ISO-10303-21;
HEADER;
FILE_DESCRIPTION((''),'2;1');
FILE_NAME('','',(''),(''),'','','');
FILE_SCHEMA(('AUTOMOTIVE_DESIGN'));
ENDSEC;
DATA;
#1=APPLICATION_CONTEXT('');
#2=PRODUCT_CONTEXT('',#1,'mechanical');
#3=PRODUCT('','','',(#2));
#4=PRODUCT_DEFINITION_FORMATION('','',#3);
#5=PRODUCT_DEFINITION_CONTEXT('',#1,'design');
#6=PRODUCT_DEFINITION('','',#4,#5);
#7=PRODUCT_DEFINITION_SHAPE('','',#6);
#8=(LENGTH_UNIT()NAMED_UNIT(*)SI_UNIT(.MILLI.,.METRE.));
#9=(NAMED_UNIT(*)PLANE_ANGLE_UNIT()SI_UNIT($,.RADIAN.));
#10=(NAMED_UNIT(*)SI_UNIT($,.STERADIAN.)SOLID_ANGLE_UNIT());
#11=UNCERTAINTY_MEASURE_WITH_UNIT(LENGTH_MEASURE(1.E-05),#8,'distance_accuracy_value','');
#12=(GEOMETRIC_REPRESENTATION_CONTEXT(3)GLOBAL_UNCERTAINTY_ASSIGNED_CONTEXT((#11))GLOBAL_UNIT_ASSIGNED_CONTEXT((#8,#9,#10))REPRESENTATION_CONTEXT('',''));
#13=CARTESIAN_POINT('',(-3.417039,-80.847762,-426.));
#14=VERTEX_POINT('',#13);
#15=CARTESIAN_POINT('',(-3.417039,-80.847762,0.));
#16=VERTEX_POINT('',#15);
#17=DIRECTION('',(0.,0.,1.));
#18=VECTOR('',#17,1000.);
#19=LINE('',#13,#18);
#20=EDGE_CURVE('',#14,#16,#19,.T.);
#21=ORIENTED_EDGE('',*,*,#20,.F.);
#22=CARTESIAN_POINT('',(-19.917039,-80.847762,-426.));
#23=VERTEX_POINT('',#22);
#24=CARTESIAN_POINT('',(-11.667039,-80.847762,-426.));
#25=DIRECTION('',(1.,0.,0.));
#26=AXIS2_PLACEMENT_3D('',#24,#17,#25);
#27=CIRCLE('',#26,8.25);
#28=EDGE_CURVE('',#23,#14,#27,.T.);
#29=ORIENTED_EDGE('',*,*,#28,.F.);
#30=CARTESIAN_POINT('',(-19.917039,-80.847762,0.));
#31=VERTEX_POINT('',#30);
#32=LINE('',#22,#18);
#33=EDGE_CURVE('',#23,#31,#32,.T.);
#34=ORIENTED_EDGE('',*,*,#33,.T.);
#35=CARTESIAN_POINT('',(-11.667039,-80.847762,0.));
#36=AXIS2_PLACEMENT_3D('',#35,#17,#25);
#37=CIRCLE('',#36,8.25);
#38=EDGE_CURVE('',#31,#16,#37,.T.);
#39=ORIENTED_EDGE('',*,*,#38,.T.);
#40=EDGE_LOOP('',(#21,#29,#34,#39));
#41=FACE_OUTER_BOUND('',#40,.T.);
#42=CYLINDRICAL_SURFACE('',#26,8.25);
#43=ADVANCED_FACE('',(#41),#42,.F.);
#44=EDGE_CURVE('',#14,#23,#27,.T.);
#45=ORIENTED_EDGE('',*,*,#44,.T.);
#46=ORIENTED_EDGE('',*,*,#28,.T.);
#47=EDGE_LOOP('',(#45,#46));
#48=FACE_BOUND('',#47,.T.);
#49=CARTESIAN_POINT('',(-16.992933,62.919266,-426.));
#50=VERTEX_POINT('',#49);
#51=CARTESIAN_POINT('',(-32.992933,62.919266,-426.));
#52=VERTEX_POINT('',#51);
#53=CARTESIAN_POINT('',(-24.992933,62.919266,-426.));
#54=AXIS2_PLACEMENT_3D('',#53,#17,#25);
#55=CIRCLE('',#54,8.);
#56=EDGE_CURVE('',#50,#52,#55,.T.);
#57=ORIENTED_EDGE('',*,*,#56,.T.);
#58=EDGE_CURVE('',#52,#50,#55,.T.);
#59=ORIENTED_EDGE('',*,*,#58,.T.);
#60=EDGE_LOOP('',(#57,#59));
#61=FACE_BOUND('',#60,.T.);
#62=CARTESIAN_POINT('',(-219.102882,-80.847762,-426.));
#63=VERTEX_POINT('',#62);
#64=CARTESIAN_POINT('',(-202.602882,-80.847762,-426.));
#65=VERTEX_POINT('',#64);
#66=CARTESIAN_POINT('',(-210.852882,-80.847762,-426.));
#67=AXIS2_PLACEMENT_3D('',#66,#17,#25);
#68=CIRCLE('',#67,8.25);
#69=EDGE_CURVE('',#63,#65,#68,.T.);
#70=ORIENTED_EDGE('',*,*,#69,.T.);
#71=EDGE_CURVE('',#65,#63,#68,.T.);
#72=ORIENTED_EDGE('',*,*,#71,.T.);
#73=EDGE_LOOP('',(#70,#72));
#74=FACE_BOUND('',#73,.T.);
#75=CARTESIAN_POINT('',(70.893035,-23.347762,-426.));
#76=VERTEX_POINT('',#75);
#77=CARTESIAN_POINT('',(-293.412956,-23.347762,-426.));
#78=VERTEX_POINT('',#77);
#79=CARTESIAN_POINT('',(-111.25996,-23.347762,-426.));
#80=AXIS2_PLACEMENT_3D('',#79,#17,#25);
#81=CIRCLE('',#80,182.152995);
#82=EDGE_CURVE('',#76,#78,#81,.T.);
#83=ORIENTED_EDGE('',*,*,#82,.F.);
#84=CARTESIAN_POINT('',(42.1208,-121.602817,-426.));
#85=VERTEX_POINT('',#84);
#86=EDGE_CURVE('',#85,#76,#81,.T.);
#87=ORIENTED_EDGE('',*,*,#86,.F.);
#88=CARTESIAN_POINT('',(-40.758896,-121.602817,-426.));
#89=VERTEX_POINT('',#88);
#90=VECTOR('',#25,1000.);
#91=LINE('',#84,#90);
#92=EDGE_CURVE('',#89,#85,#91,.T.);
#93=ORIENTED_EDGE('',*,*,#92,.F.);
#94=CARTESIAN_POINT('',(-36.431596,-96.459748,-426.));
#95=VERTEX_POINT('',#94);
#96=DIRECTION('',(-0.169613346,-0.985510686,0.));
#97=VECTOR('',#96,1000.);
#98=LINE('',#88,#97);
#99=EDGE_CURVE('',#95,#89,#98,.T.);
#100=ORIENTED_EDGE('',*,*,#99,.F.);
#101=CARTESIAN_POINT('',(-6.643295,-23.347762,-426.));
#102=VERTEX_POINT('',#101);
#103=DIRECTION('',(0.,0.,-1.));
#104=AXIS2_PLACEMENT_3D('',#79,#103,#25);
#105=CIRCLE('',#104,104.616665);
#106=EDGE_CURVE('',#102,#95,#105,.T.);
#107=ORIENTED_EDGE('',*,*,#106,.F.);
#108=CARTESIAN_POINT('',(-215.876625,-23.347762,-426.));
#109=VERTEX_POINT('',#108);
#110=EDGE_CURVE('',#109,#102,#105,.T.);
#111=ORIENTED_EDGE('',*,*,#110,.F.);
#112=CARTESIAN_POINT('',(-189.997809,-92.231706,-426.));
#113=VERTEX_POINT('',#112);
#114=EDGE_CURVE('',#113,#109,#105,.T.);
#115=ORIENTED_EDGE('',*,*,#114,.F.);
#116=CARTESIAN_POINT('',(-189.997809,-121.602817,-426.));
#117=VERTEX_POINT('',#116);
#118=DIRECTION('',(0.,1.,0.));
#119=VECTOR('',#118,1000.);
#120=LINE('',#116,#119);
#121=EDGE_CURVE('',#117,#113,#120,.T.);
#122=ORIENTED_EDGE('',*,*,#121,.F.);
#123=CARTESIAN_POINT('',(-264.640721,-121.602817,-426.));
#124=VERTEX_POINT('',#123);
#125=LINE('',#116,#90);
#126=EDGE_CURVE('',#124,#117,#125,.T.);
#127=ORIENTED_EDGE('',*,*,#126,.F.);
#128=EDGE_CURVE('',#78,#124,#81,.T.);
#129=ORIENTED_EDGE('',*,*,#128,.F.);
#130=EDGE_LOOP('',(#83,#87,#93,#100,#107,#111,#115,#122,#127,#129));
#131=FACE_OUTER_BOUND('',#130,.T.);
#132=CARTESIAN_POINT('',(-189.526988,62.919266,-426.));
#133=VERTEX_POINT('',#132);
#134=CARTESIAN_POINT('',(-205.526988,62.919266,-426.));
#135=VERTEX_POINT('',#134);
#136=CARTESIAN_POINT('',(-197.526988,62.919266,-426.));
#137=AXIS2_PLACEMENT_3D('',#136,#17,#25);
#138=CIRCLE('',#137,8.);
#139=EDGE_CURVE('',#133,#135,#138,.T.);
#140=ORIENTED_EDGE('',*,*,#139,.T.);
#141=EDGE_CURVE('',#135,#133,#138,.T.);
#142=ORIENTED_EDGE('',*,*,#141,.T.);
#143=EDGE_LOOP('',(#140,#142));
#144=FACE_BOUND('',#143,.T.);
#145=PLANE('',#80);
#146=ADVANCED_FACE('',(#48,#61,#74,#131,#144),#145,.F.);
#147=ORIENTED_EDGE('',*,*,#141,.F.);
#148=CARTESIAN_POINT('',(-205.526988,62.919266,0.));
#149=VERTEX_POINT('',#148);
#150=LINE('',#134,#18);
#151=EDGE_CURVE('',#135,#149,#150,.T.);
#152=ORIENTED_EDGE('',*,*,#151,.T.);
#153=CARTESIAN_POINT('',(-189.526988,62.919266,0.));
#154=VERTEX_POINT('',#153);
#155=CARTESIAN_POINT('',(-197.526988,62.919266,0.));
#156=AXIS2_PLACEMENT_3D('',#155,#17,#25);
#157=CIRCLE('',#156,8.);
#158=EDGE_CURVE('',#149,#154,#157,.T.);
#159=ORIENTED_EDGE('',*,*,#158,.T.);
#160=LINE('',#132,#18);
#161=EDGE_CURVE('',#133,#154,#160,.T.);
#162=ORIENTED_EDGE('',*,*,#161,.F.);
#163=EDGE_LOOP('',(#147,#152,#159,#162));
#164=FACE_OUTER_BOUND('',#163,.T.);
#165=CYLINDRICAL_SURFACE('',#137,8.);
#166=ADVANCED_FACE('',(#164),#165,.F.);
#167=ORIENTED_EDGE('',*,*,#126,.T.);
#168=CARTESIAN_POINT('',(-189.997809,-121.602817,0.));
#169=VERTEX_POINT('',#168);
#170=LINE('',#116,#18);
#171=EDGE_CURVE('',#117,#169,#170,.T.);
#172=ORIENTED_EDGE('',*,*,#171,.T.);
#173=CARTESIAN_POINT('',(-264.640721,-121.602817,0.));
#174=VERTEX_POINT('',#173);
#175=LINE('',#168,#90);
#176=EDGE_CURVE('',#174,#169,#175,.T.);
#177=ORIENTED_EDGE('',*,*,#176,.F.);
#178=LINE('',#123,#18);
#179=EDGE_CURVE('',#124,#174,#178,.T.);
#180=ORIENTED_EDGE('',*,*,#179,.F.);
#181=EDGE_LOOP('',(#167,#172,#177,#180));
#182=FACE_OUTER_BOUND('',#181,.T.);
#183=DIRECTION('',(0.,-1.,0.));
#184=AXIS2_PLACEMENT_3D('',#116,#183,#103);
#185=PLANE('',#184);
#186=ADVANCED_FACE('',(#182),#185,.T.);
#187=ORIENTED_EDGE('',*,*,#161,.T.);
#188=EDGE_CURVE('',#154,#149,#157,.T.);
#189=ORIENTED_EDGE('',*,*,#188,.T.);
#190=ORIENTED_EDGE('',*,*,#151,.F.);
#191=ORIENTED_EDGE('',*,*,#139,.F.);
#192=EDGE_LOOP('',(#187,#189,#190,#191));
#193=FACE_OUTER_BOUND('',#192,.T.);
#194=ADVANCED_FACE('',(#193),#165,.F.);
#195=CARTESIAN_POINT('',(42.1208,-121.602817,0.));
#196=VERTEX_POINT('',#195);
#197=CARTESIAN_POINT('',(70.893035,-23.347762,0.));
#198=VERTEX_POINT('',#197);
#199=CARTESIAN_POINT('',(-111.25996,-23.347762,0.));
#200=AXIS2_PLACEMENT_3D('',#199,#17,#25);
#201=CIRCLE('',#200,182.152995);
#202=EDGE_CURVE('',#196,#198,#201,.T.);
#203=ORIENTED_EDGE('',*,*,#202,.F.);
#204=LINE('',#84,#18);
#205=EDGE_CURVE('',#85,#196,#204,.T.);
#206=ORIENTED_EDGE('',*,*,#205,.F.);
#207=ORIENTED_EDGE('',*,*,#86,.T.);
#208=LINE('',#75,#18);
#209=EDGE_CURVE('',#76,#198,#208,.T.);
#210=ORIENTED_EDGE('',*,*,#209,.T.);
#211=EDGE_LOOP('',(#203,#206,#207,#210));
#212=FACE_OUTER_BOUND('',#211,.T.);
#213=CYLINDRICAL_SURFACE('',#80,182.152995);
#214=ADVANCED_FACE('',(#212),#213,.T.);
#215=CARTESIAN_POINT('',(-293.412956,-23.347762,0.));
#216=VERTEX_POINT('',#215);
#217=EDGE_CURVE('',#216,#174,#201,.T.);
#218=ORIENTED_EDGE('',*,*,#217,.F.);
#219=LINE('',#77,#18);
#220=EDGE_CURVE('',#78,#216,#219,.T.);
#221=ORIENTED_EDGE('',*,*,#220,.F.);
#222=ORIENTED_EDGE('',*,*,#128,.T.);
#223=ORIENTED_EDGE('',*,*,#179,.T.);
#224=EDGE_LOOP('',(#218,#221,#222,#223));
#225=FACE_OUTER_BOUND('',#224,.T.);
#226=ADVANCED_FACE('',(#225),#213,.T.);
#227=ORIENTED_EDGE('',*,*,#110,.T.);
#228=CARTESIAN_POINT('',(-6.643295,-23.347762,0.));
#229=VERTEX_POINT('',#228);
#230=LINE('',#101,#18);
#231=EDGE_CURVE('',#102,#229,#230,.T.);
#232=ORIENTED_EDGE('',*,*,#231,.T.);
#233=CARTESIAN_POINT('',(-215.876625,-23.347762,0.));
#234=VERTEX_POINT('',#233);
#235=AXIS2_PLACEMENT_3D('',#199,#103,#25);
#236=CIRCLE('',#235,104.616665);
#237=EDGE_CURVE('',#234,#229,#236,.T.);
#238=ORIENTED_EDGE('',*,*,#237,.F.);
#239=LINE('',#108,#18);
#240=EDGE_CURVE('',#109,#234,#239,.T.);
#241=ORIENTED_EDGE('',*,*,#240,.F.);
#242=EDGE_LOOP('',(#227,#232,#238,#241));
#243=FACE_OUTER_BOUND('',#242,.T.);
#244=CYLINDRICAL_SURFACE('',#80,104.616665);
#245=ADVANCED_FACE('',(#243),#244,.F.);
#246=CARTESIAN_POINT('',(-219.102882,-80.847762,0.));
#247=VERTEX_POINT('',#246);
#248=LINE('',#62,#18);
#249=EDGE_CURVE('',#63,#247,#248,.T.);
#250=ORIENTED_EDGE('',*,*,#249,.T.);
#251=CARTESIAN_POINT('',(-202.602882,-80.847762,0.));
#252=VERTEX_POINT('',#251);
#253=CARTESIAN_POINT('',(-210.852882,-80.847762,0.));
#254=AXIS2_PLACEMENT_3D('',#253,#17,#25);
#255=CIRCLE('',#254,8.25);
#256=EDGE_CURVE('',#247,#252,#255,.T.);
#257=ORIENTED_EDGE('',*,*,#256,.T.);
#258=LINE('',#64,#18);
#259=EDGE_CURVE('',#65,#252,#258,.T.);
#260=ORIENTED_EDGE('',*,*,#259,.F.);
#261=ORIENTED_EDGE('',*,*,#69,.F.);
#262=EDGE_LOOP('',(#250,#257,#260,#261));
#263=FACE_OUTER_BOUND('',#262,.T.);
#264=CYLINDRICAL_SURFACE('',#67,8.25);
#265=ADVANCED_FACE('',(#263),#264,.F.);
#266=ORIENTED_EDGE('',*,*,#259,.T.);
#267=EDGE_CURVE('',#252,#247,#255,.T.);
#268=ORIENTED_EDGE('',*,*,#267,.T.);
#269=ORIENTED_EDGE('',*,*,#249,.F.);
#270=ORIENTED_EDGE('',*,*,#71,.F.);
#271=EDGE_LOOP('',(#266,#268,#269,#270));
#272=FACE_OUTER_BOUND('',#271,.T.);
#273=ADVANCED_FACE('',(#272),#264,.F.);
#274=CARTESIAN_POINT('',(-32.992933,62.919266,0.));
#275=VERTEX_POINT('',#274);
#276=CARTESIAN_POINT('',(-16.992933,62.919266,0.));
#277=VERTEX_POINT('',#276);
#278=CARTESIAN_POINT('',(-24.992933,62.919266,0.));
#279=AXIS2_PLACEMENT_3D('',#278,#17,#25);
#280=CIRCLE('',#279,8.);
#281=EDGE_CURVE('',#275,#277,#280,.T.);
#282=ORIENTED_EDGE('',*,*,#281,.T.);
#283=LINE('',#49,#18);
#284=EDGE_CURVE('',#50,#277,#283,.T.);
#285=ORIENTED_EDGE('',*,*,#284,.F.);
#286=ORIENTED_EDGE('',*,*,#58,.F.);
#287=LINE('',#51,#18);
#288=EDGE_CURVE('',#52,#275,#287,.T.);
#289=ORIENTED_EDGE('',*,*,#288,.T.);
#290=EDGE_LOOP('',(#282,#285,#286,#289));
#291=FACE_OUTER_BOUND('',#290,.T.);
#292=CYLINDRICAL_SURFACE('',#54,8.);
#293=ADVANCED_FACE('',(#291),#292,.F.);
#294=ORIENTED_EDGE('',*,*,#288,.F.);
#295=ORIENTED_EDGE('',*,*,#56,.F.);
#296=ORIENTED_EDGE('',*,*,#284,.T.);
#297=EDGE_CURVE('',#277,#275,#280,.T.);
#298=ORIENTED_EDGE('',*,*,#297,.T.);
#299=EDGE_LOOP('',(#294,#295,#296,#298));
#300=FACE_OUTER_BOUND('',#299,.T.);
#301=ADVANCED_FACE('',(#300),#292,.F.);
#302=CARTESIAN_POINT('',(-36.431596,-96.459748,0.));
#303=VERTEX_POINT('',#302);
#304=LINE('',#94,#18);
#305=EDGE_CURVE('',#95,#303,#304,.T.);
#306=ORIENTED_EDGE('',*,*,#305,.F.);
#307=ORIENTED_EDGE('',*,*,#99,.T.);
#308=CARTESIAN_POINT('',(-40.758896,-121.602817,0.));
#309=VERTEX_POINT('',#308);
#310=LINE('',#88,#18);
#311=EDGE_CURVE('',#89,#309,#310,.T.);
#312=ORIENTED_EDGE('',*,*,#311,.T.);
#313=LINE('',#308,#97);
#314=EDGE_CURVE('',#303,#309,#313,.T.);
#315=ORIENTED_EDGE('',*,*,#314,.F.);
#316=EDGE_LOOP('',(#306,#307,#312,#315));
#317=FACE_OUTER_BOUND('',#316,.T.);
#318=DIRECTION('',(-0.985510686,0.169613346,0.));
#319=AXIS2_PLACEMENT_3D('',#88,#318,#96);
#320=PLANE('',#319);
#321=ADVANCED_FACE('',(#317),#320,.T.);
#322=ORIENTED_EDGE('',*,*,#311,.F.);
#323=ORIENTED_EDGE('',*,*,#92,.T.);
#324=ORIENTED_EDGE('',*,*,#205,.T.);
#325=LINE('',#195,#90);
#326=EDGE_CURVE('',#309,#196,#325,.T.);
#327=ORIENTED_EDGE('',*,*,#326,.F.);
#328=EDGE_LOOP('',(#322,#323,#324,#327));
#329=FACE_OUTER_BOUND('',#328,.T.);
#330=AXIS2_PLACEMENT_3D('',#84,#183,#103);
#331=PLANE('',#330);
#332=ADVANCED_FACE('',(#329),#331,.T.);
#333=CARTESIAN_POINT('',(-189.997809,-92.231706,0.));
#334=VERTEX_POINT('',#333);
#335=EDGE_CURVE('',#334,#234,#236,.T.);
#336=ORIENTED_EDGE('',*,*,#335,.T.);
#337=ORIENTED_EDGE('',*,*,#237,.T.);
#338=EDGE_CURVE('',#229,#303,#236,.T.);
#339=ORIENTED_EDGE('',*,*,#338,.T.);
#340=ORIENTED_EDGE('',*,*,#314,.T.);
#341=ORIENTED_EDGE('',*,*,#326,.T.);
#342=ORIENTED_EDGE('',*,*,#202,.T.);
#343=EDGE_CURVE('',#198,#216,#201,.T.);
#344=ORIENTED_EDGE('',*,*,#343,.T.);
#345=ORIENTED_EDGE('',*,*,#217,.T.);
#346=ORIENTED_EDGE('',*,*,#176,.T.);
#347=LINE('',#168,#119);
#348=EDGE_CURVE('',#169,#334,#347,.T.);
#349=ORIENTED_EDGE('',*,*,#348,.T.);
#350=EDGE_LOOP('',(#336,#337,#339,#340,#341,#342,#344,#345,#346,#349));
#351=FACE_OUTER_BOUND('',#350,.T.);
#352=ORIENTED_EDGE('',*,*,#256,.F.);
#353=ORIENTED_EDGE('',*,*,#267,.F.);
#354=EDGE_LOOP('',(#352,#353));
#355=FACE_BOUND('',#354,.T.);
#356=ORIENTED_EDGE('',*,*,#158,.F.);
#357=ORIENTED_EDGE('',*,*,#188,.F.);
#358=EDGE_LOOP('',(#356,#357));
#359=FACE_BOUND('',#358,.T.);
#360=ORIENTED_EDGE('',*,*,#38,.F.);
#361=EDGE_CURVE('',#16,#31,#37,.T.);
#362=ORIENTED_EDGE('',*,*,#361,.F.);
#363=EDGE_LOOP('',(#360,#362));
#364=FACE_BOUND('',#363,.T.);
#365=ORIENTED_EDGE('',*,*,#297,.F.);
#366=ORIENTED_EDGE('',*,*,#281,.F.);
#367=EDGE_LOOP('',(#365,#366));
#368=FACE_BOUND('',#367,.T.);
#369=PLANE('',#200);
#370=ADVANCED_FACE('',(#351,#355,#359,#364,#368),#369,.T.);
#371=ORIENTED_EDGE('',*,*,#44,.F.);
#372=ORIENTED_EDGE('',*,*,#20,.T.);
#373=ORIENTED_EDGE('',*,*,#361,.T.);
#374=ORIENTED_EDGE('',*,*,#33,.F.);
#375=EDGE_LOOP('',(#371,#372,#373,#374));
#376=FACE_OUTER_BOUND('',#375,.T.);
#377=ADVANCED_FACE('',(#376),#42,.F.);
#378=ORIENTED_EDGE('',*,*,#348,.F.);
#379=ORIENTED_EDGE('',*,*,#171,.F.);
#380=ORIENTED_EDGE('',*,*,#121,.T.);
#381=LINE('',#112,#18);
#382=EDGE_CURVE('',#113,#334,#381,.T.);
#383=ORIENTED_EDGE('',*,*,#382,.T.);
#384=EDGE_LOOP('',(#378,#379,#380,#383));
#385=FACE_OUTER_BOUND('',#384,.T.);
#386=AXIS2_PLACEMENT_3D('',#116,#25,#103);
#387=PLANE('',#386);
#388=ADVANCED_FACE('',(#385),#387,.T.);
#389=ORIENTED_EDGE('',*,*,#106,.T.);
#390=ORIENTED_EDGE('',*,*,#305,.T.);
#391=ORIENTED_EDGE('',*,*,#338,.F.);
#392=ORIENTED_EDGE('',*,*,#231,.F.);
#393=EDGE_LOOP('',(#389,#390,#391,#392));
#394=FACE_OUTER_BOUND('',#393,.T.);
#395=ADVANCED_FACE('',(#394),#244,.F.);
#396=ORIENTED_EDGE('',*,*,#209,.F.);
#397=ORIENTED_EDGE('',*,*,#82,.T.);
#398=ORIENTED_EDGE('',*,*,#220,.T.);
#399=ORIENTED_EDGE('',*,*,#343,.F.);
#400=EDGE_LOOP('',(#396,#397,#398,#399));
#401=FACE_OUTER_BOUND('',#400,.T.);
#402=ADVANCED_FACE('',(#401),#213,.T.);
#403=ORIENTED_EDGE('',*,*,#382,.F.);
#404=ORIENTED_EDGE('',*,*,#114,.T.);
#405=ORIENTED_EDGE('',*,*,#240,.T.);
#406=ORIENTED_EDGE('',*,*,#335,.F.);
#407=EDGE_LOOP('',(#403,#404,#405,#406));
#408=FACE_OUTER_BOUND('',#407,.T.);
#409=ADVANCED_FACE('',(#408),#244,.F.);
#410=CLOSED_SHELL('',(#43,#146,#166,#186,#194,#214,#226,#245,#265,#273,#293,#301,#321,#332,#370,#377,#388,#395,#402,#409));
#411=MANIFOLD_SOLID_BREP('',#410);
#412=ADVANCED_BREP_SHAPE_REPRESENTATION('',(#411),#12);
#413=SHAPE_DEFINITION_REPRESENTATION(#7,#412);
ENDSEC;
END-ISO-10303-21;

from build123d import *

# Parameters (mm, degrees)
SKETCH1_R           = 8
SKETCH1_R_2         = 8.25
BOSS_EXTRUDE1_DEPTH = 426


with BuildPart() as part:
    # Sketch1 → Boss-Extrude1 (new body)
    with BuildSketch(Plane.XY):
        with BuildLine():
            Line((-189.997809191, -121.602817484), (-189.997809191, -92.231705942))
            ThreePointArc((-189.997809191, -92.231705942), (-108.380706485, 81.229274354), (-36.431596452, -96.459748112))
            Line((-36.431596452, -96.459748112), (-40.758896177, -121.602817484))
            Line((-40.758896177, -121.602817484), (42.120800042, -121.602817484))
            ThreePointArc((42.120800042, -121.602817484), (-111.259960397, 158.805233349), (-264.640720837, -121.602817484))
            Line((-264.640720837, -121.602817484), (-189.997809191, -121.602817484))
        make_face()
        with Locations((-24.992933093, 62.919265507)):
            Circle(SKETCH1_R, mode=Mode.SUBTRACT)
        with Locations((-197.526987702, 62.919265507)):
            Circle(SKETCH1_R, mode=Mode.SUBTRACT)
        with Locations((-210.852881833, -80.847761798)):
            Circle(SKETCH1_R_2, mode=Mode.SUBTRACT)
        with Locations((-11.667038962, -80.847761798)):
            Circle(SKETCH1_R_2, mode=Mode.SUBTRACT)
    extrude(amount=-BOSS_EXTRUDE1_DEPTH)


solid = part.part
